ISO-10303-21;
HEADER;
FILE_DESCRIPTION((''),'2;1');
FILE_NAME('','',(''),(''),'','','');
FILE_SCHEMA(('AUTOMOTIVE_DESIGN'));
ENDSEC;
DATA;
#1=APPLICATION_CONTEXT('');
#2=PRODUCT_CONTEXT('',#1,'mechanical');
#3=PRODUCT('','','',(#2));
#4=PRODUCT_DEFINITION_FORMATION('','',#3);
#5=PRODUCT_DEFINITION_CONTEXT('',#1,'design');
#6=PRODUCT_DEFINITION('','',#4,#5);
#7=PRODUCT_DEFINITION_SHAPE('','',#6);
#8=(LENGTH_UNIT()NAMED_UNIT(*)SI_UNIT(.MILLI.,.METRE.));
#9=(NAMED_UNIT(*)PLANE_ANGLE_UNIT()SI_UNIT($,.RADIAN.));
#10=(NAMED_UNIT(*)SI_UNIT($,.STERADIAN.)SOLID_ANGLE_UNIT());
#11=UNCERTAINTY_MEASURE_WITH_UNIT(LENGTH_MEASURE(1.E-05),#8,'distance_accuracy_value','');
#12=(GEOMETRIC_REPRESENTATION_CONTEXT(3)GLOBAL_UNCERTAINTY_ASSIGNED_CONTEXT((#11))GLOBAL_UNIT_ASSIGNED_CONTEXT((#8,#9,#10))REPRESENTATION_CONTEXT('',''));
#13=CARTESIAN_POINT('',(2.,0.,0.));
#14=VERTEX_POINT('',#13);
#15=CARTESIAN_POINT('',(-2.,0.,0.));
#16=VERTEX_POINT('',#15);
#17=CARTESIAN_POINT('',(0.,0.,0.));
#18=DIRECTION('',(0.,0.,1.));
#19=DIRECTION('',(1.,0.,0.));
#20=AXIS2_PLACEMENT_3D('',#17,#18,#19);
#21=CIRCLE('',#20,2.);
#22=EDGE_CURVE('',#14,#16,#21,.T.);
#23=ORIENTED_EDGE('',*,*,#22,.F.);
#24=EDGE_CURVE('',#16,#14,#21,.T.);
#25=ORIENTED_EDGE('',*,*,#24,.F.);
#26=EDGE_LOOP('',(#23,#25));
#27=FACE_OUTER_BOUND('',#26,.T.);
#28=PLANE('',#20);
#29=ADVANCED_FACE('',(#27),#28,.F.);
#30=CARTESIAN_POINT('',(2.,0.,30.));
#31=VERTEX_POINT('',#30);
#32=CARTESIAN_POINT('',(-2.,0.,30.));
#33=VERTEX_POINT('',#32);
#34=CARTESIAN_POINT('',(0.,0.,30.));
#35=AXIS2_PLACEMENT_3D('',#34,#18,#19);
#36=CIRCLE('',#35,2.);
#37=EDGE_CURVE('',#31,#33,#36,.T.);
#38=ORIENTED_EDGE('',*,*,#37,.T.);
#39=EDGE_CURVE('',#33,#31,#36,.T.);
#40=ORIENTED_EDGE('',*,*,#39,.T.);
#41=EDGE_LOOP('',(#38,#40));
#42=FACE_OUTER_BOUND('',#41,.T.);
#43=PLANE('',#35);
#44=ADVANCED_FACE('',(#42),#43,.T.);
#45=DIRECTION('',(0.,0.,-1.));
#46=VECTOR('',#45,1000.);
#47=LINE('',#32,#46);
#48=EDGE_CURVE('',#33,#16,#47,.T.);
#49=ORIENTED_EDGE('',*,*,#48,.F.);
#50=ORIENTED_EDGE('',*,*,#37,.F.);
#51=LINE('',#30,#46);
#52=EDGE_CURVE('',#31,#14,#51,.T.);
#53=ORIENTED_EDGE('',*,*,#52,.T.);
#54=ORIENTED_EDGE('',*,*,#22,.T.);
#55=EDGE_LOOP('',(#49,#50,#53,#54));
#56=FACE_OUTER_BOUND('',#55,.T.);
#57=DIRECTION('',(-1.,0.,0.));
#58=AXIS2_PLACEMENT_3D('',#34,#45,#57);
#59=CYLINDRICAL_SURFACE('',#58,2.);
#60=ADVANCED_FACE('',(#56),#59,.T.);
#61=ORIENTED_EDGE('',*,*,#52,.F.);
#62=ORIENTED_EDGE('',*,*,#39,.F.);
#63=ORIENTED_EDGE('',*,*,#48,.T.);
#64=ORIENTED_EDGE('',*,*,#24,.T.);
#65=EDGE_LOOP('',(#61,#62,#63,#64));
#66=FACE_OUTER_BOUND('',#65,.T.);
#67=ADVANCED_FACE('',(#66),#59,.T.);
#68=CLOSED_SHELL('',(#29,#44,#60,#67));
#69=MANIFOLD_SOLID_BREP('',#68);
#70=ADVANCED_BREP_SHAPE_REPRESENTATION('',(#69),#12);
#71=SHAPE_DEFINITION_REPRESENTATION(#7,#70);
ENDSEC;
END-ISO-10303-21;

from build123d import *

# Parameters (mm, degrees)
PIN_PROFILE_4_R     = 2
PIN_BODY_4X30_DEPTH = 30


with BuildPart() as part:
    # Pin Profile Ø4 → Pin Body Ø4x30 (new body)
    with BuildSketch(Plane.XY):
        Circle(PIN_PROFILE_4_R)
    extrude(amount=PIN_BODY_4X30_DEPTH)


solid = part.part
